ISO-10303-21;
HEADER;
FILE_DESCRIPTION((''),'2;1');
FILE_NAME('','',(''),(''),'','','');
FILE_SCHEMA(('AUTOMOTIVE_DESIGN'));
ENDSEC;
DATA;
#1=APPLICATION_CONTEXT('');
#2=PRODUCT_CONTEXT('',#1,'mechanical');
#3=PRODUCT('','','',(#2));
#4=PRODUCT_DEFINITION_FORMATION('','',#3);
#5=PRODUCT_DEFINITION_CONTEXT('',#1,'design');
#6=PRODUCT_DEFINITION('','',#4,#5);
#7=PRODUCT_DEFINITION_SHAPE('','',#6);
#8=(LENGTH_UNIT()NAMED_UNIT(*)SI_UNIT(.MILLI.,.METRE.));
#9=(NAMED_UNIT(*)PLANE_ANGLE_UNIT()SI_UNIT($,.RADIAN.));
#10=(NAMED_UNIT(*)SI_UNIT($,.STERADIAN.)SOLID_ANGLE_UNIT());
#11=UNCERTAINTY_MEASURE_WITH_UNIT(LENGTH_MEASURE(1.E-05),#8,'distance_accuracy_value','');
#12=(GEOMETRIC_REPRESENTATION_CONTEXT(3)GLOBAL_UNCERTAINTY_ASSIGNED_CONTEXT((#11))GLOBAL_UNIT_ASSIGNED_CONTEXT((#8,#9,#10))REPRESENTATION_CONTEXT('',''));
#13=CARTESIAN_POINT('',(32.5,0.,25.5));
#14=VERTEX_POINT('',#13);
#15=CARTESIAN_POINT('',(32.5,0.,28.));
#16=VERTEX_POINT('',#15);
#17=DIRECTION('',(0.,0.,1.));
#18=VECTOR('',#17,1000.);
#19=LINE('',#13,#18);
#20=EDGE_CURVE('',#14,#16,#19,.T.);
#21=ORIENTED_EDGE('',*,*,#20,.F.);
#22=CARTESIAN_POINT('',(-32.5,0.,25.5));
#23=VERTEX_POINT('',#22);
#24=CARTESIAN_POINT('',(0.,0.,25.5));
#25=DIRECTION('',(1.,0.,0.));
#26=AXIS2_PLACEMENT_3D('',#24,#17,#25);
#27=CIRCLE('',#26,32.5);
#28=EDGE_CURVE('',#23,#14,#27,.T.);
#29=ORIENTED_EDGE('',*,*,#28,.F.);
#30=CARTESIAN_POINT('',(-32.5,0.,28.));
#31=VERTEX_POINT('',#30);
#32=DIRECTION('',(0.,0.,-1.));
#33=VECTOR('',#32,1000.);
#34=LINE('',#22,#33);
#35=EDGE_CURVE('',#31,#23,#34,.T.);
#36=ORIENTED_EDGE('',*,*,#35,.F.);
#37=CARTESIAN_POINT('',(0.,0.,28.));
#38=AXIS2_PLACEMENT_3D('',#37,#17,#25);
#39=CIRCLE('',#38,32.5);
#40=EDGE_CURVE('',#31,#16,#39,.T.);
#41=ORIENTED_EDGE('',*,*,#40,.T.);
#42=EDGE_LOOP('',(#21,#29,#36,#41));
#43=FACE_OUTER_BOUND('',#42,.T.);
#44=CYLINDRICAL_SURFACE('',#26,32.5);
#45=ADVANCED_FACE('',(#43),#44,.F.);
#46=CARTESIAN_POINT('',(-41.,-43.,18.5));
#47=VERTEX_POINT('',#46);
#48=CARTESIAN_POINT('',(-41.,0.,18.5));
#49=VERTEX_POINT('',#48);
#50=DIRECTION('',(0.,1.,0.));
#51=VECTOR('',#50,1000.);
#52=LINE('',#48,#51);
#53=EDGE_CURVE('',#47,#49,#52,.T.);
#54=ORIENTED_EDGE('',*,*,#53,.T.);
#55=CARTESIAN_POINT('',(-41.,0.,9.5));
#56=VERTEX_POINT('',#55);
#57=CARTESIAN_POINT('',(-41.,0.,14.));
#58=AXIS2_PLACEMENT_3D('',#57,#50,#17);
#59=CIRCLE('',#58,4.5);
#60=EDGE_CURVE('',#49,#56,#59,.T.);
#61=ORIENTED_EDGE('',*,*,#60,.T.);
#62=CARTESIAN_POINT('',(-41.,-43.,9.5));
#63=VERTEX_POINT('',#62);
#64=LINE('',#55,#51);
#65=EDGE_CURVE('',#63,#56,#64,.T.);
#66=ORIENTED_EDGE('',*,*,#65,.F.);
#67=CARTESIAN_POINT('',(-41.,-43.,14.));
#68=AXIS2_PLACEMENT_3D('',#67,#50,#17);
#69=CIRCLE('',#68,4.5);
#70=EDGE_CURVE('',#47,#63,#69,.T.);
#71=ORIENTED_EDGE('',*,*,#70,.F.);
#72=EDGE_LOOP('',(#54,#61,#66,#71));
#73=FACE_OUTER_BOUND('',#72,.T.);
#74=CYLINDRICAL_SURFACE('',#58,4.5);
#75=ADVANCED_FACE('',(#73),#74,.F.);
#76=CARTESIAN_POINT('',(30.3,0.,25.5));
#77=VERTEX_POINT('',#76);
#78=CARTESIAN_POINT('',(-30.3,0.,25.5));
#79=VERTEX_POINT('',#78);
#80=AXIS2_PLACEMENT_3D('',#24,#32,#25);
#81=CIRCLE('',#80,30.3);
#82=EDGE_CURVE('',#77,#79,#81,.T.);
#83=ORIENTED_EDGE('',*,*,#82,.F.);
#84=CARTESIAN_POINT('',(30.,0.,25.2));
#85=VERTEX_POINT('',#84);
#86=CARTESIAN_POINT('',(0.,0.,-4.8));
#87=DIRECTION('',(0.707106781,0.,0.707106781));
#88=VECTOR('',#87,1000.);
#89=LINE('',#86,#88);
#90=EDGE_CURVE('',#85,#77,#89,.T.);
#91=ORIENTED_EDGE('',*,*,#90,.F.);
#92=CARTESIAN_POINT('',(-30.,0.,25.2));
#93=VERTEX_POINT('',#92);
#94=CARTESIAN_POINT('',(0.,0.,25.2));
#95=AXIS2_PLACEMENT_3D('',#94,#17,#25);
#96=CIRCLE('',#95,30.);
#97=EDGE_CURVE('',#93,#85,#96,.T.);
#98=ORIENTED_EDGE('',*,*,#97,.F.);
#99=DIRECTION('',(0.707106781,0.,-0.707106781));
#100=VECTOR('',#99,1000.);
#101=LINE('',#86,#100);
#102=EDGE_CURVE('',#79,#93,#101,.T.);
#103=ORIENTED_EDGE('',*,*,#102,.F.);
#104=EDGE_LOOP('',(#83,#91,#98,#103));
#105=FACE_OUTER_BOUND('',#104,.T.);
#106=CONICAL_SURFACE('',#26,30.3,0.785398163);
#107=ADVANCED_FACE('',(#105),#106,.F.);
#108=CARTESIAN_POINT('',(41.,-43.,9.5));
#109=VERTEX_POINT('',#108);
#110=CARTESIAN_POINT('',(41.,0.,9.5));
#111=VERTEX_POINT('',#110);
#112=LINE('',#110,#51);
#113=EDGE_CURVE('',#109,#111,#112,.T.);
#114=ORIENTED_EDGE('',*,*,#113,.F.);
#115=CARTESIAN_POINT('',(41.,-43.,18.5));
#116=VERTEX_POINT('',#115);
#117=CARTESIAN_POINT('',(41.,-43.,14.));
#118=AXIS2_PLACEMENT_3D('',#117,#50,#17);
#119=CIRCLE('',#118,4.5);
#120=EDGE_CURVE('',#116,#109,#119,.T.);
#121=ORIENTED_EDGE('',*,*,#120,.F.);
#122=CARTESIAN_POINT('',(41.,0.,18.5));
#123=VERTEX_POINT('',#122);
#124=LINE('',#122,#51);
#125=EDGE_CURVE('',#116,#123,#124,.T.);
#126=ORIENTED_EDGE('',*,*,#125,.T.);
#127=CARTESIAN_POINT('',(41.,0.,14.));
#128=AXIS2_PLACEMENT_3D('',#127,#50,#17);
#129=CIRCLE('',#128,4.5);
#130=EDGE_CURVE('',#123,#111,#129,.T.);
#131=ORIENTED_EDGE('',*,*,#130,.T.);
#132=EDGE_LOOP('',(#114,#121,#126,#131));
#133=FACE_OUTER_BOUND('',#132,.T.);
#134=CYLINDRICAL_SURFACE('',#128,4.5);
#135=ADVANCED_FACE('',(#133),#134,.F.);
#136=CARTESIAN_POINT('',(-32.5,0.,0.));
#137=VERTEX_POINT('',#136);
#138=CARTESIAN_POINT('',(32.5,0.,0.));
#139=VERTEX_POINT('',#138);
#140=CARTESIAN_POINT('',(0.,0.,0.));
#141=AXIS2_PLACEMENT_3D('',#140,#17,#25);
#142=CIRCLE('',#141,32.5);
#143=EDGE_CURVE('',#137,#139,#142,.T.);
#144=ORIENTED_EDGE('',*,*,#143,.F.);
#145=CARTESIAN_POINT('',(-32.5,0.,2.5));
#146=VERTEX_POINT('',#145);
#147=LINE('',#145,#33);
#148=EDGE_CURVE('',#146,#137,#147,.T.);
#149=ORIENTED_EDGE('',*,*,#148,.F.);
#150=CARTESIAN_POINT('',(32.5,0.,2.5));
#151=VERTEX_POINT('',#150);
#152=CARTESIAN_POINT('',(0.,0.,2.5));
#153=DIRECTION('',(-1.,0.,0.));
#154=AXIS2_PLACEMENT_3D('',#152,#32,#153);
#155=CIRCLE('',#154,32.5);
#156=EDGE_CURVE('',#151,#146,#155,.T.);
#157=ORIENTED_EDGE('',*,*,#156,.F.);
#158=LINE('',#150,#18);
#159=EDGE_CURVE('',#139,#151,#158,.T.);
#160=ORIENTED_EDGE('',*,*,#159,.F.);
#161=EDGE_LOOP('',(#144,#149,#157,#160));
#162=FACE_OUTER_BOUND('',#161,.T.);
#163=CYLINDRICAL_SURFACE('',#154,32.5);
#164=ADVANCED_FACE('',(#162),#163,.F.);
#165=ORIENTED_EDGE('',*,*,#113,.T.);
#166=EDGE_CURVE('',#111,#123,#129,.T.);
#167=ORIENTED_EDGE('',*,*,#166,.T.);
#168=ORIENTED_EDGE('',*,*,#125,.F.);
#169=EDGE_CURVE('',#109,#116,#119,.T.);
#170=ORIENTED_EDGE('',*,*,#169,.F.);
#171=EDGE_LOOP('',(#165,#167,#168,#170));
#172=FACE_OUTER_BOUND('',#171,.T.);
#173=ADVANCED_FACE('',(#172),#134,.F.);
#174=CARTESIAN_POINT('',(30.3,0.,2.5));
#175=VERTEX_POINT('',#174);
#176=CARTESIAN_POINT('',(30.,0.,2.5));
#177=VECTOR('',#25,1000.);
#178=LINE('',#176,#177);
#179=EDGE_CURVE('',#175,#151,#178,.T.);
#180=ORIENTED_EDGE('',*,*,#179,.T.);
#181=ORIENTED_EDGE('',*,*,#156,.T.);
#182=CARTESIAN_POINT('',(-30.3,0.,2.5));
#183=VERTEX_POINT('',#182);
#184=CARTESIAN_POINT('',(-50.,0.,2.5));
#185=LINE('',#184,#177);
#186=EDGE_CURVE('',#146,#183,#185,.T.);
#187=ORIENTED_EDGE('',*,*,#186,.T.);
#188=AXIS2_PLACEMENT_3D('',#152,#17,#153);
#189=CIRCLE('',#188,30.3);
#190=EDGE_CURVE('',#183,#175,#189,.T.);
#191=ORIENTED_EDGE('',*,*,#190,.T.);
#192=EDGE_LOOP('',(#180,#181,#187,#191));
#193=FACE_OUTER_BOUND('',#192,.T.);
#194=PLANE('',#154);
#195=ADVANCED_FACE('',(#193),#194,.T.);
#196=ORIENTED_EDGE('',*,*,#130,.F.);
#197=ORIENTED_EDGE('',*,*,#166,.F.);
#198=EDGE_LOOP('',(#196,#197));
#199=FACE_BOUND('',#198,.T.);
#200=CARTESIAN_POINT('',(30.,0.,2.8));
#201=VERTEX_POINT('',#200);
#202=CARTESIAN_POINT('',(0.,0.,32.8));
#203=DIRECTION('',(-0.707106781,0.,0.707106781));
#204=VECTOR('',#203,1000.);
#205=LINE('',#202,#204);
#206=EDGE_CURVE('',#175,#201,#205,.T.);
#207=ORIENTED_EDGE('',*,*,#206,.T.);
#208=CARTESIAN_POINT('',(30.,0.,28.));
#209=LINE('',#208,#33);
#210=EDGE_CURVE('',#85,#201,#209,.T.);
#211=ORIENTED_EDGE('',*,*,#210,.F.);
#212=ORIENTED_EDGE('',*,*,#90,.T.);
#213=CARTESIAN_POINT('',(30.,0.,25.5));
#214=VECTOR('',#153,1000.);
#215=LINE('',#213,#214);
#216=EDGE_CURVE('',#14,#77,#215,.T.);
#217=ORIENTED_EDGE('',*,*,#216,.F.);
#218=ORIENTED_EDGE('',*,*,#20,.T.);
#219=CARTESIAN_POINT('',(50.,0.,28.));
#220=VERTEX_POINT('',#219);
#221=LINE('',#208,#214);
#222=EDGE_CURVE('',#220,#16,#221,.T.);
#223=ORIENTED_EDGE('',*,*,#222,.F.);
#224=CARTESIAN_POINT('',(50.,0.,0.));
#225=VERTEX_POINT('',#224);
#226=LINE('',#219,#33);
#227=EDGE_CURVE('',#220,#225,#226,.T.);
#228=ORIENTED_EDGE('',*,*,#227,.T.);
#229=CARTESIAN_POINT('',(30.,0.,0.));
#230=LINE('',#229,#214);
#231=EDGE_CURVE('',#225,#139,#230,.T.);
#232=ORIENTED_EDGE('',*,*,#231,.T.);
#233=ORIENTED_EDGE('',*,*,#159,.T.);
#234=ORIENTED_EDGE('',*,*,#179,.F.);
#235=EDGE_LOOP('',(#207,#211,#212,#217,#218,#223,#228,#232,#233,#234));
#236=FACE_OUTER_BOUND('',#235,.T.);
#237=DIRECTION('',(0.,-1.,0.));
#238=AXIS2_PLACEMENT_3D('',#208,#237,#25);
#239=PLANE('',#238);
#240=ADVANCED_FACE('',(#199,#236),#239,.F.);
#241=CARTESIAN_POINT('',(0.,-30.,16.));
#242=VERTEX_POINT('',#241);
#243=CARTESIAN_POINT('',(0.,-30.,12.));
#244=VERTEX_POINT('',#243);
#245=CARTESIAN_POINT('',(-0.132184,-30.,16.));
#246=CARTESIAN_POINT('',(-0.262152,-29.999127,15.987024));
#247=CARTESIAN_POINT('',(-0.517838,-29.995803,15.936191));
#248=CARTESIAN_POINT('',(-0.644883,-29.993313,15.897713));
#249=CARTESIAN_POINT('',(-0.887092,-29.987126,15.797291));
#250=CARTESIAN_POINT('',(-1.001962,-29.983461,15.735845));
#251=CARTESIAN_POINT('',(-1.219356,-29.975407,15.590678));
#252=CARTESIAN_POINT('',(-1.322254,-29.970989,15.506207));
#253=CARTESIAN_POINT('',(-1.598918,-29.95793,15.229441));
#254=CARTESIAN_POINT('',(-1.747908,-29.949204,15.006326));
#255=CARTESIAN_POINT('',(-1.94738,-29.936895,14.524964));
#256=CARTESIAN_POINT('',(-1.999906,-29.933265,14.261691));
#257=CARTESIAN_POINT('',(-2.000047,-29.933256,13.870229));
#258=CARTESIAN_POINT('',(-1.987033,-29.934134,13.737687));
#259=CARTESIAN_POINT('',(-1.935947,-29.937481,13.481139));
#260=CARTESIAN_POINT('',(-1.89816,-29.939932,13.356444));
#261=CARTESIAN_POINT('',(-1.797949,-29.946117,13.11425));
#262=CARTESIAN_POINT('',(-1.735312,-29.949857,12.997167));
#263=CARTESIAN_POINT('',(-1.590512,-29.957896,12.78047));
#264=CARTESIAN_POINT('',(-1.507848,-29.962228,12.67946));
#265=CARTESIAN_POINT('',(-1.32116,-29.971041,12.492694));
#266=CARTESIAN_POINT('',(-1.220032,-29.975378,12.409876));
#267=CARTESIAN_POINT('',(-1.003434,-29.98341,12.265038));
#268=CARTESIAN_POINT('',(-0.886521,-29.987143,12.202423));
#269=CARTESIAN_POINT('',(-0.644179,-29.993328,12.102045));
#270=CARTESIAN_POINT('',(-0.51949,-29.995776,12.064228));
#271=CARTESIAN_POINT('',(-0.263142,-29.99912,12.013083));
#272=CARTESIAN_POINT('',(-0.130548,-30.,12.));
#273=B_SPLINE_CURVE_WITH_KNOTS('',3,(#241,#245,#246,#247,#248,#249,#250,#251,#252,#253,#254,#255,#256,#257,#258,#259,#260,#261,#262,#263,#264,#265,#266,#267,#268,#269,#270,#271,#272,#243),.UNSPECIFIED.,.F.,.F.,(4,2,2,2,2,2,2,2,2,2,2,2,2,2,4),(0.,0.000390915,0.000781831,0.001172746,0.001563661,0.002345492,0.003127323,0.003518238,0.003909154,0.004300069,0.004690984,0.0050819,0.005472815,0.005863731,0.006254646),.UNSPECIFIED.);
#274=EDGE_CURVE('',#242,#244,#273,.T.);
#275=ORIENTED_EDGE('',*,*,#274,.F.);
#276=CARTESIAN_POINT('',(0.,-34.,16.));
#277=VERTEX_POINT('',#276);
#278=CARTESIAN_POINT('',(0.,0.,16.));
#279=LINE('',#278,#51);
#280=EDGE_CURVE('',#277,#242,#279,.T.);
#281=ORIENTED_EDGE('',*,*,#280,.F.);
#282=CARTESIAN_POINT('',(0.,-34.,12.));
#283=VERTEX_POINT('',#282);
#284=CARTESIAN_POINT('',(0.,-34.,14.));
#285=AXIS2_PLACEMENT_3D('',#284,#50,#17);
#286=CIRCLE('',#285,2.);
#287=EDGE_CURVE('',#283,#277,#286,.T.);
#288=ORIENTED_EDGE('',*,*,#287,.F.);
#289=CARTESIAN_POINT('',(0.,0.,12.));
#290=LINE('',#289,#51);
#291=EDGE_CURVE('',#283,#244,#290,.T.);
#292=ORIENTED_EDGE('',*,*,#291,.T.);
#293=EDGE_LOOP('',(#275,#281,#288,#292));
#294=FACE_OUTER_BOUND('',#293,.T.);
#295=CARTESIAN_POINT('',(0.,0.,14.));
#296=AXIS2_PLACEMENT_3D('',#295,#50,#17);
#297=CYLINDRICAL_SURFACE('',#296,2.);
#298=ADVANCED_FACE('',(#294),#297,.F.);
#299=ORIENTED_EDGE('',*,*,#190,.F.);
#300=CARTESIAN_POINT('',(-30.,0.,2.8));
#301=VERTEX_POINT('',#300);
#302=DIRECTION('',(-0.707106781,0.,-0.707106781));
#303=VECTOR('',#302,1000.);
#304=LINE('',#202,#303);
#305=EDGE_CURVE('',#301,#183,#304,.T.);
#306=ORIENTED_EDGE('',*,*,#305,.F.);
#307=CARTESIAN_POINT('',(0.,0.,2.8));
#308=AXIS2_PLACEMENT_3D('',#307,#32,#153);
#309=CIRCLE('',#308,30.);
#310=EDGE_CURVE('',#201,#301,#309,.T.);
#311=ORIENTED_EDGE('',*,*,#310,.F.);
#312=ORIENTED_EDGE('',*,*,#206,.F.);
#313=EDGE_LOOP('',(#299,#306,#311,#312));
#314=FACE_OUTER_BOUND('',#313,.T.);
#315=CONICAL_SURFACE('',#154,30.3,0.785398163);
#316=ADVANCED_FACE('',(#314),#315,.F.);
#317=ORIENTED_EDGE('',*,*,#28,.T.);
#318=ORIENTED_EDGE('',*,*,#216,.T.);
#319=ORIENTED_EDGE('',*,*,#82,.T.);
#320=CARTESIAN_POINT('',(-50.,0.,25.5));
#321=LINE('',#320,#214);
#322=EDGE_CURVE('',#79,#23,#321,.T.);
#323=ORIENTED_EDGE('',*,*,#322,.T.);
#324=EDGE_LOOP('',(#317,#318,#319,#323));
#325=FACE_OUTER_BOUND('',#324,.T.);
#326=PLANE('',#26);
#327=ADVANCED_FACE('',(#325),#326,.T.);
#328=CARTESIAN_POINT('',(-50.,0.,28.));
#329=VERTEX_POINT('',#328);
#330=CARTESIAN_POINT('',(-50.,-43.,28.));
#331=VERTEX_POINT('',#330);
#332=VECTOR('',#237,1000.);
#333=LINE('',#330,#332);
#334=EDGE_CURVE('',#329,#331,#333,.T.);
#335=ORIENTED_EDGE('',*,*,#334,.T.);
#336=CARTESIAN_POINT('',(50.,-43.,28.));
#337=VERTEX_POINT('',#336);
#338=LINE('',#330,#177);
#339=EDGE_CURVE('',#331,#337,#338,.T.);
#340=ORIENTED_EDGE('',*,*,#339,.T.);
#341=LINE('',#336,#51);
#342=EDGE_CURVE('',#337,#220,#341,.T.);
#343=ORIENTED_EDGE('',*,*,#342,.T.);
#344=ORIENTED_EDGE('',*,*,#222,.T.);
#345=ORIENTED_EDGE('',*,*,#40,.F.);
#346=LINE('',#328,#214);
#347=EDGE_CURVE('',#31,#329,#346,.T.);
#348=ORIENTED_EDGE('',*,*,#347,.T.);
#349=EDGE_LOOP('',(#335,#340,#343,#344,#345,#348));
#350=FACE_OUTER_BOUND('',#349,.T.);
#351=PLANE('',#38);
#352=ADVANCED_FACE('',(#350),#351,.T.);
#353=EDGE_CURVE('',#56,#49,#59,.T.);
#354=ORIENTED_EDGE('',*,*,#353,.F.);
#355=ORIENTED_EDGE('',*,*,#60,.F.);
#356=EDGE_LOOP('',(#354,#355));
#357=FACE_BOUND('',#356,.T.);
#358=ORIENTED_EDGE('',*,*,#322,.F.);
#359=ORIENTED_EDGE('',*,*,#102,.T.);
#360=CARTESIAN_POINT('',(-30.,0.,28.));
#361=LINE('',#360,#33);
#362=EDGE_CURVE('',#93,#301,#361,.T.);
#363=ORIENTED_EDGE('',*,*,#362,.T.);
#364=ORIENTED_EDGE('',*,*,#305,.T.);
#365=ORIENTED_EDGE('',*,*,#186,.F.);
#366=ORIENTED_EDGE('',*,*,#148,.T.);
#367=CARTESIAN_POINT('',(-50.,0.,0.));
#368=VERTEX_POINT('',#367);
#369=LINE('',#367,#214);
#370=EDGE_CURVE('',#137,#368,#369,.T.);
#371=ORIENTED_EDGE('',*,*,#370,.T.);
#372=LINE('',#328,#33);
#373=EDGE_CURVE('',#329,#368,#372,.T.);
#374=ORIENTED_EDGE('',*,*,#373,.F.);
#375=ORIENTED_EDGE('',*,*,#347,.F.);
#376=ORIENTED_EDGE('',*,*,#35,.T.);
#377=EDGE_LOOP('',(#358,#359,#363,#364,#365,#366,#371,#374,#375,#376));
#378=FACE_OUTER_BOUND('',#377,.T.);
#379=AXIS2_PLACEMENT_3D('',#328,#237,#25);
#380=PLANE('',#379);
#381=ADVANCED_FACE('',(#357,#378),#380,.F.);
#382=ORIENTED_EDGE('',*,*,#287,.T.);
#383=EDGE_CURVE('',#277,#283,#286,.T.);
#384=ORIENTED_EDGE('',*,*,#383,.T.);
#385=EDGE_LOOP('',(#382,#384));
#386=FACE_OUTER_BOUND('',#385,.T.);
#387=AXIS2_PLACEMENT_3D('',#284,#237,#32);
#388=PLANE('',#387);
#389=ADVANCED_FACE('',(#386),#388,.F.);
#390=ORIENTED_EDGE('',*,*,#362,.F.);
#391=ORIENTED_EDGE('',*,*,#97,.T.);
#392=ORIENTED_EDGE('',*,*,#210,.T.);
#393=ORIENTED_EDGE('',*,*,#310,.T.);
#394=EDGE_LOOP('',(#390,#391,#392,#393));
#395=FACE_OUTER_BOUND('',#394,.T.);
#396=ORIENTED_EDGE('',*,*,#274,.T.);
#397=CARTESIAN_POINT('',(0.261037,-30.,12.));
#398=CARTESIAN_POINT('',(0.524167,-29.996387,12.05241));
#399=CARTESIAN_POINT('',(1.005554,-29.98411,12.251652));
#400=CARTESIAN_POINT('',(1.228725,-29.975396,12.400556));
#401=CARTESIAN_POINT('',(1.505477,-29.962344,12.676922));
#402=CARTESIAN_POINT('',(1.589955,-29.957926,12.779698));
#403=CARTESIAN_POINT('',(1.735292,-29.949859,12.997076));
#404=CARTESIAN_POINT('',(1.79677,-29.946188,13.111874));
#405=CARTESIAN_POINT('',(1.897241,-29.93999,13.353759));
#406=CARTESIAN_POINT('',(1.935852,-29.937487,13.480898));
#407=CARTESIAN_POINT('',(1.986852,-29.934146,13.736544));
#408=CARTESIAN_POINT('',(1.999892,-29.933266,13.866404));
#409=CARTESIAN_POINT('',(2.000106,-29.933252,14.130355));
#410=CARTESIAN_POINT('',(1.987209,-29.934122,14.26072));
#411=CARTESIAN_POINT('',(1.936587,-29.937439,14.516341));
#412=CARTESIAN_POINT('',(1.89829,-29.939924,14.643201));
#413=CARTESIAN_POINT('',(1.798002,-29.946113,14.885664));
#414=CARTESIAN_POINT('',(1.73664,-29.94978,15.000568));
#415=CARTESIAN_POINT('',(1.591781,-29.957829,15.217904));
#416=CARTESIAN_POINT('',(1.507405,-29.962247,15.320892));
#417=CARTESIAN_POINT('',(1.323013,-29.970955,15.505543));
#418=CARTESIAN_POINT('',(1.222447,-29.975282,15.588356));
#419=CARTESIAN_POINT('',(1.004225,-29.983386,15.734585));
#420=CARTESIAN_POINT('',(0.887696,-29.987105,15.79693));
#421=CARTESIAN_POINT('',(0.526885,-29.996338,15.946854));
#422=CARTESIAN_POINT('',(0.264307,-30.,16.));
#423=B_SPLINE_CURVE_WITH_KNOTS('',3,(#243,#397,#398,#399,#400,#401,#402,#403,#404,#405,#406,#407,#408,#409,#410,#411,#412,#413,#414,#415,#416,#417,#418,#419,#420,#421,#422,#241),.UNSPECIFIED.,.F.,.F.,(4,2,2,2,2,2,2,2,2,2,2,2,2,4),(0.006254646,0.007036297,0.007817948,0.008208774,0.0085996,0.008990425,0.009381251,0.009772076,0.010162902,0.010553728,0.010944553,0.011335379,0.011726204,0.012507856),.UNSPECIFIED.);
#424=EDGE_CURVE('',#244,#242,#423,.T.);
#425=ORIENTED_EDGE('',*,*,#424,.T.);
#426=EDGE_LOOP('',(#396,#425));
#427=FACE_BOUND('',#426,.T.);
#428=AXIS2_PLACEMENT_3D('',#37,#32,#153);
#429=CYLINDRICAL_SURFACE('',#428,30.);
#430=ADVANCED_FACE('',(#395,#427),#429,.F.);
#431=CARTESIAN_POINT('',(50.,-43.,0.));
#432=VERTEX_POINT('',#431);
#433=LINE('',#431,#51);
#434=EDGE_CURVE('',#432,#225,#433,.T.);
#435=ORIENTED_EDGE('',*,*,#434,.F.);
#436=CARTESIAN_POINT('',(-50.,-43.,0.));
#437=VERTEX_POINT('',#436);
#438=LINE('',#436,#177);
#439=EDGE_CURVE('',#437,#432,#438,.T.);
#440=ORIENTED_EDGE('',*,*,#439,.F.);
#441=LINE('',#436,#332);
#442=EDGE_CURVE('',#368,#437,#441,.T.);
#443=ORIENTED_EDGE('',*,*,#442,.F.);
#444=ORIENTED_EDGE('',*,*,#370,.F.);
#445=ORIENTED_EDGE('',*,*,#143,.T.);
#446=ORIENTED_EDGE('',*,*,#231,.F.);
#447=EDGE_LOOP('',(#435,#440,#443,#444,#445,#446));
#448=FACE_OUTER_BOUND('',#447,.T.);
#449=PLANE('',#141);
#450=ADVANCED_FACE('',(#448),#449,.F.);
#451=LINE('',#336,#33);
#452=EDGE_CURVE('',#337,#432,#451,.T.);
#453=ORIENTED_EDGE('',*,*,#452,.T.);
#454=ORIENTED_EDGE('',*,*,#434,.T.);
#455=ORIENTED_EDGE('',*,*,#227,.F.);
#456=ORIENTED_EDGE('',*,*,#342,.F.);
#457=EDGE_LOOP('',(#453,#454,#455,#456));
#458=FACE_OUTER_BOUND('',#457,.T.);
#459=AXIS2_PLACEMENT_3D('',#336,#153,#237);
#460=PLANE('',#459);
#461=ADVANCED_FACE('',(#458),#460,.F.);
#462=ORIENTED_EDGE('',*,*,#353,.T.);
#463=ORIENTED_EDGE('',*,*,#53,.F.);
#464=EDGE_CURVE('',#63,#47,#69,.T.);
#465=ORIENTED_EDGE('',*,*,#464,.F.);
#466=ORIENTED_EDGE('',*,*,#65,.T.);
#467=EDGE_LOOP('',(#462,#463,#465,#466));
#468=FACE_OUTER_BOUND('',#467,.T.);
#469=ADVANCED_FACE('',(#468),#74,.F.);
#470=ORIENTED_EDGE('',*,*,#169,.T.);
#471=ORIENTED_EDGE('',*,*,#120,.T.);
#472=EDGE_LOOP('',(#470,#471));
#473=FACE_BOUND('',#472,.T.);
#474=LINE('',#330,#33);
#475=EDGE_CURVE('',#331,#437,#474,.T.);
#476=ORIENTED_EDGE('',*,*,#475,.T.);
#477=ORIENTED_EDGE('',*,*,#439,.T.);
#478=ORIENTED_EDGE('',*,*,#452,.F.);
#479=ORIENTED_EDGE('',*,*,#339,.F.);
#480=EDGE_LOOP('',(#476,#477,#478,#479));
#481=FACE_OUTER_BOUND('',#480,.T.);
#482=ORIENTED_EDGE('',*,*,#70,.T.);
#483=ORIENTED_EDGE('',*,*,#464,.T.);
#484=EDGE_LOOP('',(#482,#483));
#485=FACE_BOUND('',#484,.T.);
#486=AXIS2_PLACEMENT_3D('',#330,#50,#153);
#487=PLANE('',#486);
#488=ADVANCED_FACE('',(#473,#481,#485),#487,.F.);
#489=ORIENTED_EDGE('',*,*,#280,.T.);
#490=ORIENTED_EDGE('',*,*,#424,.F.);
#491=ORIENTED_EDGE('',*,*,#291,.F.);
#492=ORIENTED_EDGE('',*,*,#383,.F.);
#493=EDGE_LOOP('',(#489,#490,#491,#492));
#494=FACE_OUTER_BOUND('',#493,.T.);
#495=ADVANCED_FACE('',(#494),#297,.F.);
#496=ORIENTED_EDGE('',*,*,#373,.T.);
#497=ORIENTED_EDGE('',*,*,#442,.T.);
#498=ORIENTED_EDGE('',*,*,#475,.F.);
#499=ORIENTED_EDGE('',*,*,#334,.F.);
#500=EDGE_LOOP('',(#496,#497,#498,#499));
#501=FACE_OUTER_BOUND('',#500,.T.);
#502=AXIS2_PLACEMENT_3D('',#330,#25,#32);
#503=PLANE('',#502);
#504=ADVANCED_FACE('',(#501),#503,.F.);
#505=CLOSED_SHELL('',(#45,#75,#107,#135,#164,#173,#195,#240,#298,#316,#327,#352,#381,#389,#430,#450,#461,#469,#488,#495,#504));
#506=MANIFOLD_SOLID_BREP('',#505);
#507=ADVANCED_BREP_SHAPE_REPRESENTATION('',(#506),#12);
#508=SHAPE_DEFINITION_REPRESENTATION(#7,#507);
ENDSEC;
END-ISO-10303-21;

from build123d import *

# Parameters (mm, degrees)
BOSS_EXTRUDE1_DEPTH = 28
SKETCH2_R           = 32.5
CUT_EXTRUDE1_DEPTH  = 2.5
CUT_EXTRUDE2_START  = -2.5
SKETCH3_R           = 32.5
CUT_EXTRUDE2_DEPTH  = 2.5
CHAMFER1_SIZE       = 0.3
HOLE1_D             = 9
HOLE2_D             = 4
HOLE2_DEPTH         = 34


with BuildPart() as part:
    # Sketch1 → Boss-Extrude1 (new body)
    with BuildSketch(Plane.XY):
        with BuildLine():
            Line((-50, 0), (-30, 0))
            ThreePointArc((-30, 0), (0, -30), (30, 0))
            Line((30, 0), (50, 0))
            Line((50, 0), (50, -43))
            Line((50, -43), (-50, -43))
            Line((-50, -43), (-50, 0))
        make_face()
    extrude(amount=BOSS_EXTRUDE1_DEPTH)

    # Sketch2 → Cut-Extrude1 (cut)
    with BuildSketch(Plane.XY.offset(28)):
        Circle(SKETCH2_R)
    extrude(amount=-CUT_EXTRUDE1_DEPTH, mode=Mode.SUBTRACT)

    # Sketch3 → Cut-Extrude2 (cut)
    with BuildSketch(Plane(origin=(0, 0, 0), x_dir=(-1, 0, 0), z_dir=(0, 0, -1)).offset(CUT_EXTRUDE2_START)):
        Circle(SKETCH3_R)
    extrude(amount=CUT_EXTRUDE2_DEPTH, mode=Mode.SUBTRACT)

    # Chamfer1
    chamfer1_edges = [part.edges().sort_by_distance(p)[0] for p in [
        (0, -30, 25.5),
        (0, -30, 2.5),
    ]]
    chamfer(chamfer1_edges, length=CHAMFER1_SIZE)

    # Hole1 (through all)
    with Locations(Plane(origin=(0, 0, 0), x_dir=(1, 0, 0), z_dir=(0, 1, 0))):
        with Locations((-41, -14), (41, -14)):
            Hole(HOLE1_D / 2)

    # Hole2
    with Locations(Plane(origin=(0, 0, 0), x_dir=(1, 0, 0), z_dir=(0, 1, 0))):
        with Locations((0, -14)):
            Hole(HOLE2_D / 2, depth=HOLE2_DEPTH)


solid = part.part
